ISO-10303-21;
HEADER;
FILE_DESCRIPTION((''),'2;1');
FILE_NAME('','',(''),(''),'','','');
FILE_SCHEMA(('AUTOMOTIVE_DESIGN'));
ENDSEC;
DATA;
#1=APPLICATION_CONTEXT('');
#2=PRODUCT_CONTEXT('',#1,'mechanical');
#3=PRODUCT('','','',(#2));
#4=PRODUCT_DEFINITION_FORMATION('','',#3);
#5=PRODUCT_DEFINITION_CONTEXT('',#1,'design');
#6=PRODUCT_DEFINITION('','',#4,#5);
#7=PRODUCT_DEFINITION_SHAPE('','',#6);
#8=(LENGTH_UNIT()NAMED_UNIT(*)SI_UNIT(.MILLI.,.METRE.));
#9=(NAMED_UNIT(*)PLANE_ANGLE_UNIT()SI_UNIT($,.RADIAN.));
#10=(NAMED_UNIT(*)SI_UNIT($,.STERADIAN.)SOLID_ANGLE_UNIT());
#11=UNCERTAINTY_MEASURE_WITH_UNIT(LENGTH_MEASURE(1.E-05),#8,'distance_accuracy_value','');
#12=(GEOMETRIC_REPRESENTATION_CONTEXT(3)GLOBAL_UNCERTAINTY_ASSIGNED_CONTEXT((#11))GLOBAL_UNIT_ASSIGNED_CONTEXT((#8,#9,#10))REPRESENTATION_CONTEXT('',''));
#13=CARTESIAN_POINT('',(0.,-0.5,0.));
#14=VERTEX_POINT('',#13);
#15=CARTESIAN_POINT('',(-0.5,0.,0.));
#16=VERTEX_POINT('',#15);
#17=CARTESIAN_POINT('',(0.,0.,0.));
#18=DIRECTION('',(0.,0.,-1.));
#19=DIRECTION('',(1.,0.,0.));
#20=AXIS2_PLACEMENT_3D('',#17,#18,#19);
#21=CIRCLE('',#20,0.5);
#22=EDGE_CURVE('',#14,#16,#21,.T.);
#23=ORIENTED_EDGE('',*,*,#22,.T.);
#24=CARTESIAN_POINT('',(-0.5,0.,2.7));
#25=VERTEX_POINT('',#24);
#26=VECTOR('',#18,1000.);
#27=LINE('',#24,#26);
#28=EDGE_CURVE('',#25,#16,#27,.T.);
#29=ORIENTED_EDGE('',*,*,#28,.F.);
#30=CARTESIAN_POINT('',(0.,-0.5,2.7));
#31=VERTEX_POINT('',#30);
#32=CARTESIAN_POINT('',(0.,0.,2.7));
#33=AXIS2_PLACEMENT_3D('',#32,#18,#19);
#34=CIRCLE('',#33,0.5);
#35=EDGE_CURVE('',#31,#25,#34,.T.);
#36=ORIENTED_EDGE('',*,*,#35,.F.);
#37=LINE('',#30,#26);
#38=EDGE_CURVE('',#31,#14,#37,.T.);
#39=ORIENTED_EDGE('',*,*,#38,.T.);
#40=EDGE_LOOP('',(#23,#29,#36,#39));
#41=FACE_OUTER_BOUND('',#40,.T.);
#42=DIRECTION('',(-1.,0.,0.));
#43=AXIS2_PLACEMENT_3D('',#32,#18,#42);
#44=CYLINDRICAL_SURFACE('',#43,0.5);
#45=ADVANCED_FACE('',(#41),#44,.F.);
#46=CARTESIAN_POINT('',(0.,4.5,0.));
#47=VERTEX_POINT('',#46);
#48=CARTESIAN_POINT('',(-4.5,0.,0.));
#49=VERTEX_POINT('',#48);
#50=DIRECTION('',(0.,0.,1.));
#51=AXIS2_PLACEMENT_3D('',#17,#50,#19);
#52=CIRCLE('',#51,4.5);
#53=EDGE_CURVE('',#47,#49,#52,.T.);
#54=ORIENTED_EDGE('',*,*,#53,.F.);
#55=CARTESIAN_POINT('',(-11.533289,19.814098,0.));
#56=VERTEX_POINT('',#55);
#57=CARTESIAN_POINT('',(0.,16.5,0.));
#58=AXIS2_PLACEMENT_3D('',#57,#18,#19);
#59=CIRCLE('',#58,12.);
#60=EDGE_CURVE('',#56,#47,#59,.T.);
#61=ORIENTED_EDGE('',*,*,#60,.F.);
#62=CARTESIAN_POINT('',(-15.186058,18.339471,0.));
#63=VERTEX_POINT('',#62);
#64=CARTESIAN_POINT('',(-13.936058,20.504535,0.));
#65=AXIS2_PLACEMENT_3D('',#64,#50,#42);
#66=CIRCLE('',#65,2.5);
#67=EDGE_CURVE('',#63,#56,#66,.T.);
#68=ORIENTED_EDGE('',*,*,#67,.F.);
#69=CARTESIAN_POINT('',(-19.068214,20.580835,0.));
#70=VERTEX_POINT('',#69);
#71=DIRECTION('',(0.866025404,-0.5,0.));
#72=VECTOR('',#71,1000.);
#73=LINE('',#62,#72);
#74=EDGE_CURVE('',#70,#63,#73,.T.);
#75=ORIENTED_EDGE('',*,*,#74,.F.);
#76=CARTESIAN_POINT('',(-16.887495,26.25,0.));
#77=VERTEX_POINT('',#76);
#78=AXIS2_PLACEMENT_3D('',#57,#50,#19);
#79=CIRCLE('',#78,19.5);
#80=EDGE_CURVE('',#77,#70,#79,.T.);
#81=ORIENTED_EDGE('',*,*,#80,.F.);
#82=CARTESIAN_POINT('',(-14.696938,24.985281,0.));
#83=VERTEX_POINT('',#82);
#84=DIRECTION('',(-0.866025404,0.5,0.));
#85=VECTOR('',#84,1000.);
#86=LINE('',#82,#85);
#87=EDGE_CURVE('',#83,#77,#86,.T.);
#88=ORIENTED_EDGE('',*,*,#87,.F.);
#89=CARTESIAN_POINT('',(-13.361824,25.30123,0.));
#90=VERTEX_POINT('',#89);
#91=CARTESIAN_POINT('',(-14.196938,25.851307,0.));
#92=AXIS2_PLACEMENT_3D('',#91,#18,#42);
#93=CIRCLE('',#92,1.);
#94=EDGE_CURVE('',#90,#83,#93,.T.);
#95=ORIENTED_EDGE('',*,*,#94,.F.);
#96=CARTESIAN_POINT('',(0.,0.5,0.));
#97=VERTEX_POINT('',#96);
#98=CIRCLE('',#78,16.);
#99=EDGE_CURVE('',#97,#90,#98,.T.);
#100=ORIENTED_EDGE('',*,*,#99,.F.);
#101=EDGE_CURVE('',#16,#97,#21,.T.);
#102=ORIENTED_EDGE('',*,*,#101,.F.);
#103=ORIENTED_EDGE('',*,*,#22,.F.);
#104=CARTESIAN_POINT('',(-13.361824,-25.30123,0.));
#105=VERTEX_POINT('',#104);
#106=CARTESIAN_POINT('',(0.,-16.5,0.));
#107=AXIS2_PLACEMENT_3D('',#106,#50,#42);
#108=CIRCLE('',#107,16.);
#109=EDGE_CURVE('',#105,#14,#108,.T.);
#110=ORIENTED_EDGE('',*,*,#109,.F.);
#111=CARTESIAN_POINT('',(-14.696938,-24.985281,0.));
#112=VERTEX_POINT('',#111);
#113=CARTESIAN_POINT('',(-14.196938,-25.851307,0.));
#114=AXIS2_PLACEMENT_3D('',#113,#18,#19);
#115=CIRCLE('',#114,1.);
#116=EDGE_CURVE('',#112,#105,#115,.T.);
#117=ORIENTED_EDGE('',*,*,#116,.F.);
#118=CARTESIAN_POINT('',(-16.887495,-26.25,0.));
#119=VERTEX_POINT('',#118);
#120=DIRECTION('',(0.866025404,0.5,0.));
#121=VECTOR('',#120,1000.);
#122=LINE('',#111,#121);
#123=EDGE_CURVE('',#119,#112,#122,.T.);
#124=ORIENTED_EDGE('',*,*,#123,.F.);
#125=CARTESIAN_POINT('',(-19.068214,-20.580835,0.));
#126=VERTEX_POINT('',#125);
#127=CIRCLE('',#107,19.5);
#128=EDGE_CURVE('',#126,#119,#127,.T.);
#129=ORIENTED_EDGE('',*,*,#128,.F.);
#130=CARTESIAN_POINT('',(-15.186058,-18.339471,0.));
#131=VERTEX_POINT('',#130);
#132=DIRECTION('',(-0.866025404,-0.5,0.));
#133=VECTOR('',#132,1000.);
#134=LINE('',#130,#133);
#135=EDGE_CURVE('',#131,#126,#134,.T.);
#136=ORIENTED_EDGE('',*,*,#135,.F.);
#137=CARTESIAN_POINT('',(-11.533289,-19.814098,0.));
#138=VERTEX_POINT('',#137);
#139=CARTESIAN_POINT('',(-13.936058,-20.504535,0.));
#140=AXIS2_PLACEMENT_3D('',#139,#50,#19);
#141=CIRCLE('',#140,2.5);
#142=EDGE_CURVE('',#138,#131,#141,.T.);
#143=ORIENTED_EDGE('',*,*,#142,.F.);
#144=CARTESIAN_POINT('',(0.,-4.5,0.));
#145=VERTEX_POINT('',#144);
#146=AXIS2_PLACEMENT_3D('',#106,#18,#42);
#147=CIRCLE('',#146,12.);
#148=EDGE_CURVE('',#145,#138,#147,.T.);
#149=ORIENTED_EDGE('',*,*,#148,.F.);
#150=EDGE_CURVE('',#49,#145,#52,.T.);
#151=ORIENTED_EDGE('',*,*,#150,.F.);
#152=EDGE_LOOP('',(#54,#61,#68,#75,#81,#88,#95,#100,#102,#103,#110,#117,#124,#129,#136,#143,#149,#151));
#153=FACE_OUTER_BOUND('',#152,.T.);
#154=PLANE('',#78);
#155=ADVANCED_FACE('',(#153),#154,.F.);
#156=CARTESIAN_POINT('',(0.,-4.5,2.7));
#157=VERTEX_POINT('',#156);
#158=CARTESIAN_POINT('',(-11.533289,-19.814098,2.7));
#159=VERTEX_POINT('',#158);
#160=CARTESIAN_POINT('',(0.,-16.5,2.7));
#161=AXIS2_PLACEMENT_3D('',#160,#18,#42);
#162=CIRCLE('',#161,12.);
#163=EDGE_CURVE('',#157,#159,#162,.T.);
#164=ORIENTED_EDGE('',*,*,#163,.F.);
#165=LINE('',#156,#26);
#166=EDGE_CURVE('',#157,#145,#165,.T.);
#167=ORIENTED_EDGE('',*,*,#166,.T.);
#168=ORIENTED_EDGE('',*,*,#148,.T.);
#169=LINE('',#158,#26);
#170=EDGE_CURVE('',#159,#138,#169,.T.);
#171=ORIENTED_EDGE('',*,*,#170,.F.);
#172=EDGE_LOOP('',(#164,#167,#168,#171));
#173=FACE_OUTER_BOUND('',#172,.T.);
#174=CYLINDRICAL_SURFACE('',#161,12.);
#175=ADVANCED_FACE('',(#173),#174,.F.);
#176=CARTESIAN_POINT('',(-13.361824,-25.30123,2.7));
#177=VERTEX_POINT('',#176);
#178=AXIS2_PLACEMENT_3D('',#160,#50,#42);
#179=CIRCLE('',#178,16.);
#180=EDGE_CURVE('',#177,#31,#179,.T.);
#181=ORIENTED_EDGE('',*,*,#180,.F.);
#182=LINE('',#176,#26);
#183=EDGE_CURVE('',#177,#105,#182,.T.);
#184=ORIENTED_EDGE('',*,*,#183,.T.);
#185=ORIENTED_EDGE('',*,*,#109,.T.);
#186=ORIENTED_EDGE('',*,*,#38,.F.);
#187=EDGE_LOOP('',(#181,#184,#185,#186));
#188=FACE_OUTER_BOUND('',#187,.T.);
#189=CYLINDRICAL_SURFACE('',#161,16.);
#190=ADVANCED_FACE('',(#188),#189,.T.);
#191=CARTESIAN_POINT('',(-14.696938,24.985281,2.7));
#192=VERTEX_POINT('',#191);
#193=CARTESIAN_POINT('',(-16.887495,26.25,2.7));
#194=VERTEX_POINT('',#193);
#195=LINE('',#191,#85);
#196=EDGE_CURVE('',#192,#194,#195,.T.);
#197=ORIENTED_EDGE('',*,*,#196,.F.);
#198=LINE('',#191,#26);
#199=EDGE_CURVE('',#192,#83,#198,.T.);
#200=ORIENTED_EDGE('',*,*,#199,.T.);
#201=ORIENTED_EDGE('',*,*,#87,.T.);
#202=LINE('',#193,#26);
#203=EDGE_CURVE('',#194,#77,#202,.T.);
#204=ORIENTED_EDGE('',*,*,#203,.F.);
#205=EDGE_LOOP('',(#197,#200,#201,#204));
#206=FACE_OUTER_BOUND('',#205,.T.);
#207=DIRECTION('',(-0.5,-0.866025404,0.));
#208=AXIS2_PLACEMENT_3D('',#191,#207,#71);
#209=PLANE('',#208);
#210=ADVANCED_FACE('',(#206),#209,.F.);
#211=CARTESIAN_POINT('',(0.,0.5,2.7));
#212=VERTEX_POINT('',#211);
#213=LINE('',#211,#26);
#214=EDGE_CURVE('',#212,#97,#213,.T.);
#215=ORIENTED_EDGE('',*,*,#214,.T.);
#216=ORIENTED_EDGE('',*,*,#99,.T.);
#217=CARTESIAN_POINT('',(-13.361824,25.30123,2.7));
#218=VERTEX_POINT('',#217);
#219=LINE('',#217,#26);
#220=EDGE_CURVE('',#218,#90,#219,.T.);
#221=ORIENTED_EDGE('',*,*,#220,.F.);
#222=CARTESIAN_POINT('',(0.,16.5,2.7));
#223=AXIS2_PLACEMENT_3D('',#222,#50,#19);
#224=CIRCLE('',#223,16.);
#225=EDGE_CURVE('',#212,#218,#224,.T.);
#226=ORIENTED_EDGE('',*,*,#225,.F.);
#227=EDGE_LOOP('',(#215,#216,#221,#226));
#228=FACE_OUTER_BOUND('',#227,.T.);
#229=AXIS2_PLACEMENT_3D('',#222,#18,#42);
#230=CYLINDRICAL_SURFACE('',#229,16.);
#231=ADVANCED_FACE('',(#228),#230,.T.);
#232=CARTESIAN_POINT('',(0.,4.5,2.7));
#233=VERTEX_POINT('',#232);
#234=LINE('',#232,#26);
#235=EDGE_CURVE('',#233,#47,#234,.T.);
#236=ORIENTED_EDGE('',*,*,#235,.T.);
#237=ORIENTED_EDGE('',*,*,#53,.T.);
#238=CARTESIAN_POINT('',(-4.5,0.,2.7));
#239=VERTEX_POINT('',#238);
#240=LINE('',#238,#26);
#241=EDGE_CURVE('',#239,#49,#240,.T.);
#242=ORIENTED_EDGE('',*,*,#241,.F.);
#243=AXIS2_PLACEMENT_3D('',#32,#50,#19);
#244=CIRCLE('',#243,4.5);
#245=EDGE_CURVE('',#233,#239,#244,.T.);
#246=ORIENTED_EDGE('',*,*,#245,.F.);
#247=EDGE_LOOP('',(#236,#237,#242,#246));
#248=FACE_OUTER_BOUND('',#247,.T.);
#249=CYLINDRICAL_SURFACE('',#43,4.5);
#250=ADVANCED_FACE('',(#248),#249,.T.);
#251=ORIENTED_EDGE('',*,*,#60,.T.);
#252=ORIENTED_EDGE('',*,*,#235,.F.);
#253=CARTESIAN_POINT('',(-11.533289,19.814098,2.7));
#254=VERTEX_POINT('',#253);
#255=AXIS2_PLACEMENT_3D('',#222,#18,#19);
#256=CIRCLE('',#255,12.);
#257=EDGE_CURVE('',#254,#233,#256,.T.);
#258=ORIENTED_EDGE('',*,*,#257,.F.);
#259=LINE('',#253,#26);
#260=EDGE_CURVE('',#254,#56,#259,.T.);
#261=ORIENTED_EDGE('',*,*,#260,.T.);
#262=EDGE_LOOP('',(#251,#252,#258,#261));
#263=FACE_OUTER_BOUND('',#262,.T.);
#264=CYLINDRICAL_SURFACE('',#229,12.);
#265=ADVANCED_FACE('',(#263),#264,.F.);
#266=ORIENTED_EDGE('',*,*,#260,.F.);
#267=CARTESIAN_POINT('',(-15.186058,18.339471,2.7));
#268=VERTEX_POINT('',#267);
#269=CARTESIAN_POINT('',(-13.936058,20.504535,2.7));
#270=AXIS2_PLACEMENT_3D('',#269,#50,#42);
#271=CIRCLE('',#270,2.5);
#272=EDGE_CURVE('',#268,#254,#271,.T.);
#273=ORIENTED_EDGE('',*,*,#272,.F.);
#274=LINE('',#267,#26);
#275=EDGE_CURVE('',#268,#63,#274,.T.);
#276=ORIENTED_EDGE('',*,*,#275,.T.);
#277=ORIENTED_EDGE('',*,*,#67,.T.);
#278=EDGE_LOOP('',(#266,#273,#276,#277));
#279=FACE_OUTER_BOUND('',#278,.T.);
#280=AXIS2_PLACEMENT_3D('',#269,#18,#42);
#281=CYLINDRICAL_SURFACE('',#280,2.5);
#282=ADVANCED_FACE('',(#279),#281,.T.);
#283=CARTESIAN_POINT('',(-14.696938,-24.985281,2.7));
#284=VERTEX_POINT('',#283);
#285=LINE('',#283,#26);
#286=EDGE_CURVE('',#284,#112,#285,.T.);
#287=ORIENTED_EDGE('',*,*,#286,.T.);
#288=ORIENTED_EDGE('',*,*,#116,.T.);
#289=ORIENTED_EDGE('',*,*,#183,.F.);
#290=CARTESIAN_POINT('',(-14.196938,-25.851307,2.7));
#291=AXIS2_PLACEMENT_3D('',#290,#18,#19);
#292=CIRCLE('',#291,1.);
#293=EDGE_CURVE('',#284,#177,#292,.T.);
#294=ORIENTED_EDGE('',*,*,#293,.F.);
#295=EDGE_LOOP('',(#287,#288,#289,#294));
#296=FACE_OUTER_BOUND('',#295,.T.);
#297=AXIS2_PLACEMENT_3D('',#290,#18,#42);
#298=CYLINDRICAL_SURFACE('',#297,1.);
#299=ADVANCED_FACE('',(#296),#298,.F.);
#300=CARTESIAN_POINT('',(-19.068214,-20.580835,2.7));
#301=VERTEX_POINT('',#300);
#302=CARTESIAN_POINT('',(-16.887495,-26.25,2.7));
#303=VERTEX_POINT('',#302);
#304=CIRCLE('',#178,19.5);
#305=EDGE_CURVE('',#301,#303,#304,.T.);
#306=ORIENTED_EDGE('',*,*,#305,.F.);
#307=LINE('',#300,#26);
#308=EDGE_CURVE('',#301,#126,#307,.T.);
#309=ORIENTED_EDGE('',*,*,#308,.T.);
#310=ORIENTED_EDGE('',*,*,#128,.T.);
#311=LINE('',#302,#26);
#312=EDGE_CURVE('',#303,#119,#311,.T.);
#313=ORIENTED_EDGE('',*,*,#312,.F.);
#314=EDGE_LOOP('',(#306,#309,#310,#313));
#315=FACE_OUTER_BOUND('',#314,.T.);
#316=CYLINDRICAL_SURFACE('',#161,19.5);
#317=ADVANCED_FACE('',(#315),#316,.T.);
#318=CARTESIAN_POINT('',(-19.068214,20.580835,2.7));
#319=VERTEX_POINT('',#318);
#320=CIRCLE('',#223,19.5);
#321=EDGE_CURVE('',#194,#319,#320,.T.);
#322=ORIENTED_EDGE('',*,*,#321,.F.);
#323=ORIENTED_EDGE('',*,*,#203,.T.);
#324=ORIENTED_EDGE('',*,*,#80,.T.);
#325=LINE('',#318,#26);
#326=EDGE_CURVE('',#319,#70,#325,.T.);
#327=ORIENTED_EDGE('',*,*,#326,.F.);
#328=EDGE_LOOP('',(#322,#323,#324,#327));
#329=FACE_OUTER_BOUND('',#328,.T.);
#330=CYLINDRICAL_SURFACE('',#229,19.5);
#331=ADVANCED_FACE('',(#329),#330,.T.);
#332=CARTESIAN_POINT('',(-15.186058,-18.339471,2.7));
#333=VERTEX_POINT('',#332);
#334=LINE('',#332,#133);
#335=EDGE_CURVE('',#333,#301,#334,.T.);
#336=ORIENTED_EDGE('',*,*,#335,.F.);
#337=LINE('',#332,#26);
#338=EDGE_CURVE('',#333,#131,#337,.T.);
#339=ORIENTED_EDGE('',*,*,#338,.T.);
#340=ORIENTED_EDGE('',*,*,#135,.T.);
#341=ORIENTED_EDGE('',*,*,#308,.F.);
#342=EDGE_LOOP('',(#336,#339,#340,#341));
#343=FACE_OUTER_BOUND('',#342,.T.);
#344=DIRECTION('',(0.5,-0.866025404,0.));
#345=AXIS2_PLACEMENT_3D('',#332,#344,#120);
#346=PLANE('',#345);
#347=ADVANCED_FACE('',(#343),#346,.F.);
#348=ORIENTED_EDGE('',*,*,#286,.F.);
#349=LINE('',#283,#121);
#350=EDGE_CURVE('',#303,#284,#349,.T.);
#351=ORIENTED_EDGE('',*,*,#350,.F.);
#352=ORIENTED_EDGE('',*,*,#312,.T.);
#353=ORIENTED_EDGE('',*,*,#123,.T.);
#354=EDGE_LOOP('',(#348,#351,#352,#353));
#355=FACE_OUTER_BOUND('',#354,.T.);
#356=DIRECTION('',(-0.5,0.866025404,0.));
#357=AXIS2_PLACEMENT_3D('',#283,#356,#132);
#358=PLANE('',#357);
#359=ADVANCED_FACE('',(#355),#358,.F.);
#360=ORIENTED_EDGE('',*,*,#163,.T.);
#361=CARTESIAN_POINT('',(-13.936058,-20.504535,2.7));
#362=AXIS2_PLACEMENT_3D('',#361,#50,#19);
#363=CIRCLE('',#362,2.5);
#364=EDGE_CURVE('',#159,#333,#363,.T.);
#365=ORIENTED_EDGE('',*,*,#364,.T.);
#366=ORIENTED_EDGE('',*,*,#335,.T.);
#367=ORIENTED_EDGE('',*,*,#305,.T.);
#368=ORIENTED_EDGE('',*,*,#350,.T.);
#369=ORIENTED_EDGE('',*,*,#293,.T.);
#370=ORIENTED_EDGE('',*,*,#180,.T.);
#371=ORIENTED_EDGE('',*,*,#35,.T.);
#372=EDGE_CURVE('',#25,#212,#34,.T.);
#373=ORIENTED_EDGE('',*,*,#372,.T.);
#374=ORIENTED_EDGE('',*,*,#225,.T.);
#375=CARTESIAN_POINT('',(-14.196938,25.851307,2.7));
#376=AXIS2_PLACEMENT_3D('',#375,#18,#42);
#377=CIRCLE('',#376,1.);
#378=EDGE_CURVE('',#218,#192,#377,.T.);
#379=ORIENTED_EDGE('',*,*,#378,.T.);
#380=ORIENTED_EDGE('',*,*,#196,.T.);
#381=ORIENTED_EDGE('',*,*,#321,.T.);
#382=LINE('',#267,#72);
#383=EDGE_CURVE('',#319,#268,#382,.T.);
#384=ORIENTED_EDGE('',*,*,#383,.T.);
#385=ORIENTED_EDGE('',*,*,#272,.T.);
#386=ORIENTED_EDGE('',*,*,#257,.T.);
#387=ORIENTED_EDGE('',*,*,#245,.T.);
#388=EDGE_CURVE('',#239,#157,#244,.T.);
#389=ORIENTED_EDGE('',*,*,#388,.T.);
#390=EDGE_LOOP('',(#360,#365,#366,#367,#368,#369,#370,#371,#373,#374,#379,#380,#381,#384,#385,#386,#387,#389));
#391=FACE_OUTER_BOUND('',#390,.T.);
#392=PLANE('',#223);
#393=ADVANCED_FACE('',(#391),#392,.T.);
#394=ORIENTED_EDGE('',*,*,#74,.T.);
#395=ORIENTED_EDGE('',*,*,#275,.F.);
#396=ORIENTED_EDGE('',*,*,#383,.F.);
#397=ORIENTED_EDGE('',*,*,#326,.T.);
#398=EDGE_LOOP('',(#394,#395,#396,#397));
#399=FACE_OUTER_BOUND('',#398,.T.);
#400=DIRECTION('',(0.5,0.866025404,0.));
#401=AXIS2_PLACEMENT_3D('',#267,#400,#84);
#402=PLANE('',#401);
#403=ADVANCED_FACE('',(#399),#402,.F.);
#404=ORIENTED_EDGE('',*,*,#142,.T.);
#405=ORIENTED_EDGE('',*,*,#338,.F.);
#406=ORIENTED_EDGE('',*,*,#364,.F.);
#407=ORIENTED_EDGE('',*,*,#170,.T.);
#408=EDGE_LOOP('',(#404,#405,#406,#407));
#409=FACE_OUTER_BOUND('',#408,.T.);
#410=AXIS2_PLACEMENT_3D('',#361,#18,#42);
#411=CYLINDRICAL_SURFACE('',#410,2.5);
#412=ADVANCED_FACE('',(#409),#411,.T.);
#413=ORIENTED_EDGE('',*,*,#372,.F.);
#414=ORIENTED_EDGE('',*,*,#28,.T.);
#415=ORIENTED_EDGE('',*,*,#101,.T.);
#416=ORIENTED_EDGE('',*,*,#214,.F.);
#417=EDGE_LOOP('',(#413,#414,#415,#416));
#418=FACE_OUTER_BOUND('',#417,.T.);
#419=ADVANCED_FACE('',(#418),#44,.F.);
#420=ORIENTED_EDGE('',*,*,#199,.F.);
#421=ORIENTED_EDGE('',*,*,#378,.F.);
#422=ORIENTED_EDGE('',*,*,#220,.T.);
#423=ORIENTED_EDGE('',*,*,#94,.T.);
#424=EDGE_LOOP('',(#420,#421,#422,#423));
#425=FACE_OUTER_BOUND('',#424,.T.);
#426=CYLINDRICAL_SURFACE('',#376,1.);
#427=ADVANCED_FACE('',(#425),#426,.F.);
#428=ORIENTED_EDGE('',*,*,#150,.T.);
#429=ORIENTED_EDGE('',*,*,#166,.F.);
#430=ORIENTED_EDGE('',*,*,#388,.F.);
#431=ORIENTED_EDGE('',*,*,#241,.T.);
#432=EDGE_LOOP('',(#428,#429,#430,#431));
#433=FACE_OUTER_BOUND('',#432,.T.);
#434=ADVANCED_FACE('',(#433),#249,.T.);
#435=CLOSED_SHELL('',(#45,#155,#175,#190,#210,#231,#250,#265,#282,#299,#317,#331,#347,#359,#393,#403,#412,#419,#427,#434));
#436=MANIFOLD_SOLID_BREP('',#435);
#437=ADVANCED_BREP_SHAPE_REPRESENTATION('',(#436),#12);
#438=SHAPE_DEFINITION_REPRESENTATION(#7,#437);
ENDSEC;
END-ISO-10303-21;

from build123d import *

# Parameters (mm, degrees)
BOSS_EXTRUDE1_DEPTH = 2.7


with BuildPart() as part:
    # Sketch1 → Boss-Extrude1 (new body)
    with BuildSketch(Plane.XY):
        with BuildLine():
            Line((-14.696938457, 24.985281374), (-16.887495374, 26.25))
            ThreePointArc((-16.887495374, 26.25), (-18.199948236, 23.500848821), (-19.068213964, 20.580835235))
            Line((-19.068213964, 20.580835235), (-15.186057607, 18.339471217))
            ThreePointArc((-15.186057607, 18.339471217), (-13.000189211, 18.186313351), (-11.533289054, 19.814097705))
            ThreePointArc((-11.533289054, 19.814097705), (9.5856448, 23.719100621), (0, 4.5))
            ThreePointArc((0, 4.5), (-4.5, 0), (0, -4.5))
            ThreePointArc((0, -4.5), (9.5856448, -23.719100621), (-11.533289054, -19.814097705))
            ThreePointArc((-11.533289054, -19.814097705), (-13.000189211, -18.186313351), (-15.186057607, -18.339471217))
            Line((-15.186057607, -18.339471217), (-19.068213964, -20.580835235))
            ThreePointArc((-19.068213964, -20.580835235), (-18.199948236, -23.500848821), (-16.887495374, -26.25))
            Line((-16.887495374, -26.25), (-14.696938457, -24.985281374))
            ThreePointArc((-14.696938457, -24.985281374), (-13.966653368, -24.87818357), (-13.36182443, -25.301229909))
            ThreePointArc((-13.36182443, -25.301229909), (14.085802756, -24.088818138), (0, -0.5))
            ThreePointArc((0, -0.5), (-0.5, 0), (0, 0.5))
            ThreePointArc((0, 0.5), (14.085802756, 24.088818138), (-13.36182443, 25.301229909))
            ThreePointArc((-13.36182443, 25.301229909), (-13.966653368, 24.87818357), (-14.696938457, 24.985281374))
        make_face()
    extrude(amount=BOSS_EXTRUDE1_DEPTH)


solid = part.part
